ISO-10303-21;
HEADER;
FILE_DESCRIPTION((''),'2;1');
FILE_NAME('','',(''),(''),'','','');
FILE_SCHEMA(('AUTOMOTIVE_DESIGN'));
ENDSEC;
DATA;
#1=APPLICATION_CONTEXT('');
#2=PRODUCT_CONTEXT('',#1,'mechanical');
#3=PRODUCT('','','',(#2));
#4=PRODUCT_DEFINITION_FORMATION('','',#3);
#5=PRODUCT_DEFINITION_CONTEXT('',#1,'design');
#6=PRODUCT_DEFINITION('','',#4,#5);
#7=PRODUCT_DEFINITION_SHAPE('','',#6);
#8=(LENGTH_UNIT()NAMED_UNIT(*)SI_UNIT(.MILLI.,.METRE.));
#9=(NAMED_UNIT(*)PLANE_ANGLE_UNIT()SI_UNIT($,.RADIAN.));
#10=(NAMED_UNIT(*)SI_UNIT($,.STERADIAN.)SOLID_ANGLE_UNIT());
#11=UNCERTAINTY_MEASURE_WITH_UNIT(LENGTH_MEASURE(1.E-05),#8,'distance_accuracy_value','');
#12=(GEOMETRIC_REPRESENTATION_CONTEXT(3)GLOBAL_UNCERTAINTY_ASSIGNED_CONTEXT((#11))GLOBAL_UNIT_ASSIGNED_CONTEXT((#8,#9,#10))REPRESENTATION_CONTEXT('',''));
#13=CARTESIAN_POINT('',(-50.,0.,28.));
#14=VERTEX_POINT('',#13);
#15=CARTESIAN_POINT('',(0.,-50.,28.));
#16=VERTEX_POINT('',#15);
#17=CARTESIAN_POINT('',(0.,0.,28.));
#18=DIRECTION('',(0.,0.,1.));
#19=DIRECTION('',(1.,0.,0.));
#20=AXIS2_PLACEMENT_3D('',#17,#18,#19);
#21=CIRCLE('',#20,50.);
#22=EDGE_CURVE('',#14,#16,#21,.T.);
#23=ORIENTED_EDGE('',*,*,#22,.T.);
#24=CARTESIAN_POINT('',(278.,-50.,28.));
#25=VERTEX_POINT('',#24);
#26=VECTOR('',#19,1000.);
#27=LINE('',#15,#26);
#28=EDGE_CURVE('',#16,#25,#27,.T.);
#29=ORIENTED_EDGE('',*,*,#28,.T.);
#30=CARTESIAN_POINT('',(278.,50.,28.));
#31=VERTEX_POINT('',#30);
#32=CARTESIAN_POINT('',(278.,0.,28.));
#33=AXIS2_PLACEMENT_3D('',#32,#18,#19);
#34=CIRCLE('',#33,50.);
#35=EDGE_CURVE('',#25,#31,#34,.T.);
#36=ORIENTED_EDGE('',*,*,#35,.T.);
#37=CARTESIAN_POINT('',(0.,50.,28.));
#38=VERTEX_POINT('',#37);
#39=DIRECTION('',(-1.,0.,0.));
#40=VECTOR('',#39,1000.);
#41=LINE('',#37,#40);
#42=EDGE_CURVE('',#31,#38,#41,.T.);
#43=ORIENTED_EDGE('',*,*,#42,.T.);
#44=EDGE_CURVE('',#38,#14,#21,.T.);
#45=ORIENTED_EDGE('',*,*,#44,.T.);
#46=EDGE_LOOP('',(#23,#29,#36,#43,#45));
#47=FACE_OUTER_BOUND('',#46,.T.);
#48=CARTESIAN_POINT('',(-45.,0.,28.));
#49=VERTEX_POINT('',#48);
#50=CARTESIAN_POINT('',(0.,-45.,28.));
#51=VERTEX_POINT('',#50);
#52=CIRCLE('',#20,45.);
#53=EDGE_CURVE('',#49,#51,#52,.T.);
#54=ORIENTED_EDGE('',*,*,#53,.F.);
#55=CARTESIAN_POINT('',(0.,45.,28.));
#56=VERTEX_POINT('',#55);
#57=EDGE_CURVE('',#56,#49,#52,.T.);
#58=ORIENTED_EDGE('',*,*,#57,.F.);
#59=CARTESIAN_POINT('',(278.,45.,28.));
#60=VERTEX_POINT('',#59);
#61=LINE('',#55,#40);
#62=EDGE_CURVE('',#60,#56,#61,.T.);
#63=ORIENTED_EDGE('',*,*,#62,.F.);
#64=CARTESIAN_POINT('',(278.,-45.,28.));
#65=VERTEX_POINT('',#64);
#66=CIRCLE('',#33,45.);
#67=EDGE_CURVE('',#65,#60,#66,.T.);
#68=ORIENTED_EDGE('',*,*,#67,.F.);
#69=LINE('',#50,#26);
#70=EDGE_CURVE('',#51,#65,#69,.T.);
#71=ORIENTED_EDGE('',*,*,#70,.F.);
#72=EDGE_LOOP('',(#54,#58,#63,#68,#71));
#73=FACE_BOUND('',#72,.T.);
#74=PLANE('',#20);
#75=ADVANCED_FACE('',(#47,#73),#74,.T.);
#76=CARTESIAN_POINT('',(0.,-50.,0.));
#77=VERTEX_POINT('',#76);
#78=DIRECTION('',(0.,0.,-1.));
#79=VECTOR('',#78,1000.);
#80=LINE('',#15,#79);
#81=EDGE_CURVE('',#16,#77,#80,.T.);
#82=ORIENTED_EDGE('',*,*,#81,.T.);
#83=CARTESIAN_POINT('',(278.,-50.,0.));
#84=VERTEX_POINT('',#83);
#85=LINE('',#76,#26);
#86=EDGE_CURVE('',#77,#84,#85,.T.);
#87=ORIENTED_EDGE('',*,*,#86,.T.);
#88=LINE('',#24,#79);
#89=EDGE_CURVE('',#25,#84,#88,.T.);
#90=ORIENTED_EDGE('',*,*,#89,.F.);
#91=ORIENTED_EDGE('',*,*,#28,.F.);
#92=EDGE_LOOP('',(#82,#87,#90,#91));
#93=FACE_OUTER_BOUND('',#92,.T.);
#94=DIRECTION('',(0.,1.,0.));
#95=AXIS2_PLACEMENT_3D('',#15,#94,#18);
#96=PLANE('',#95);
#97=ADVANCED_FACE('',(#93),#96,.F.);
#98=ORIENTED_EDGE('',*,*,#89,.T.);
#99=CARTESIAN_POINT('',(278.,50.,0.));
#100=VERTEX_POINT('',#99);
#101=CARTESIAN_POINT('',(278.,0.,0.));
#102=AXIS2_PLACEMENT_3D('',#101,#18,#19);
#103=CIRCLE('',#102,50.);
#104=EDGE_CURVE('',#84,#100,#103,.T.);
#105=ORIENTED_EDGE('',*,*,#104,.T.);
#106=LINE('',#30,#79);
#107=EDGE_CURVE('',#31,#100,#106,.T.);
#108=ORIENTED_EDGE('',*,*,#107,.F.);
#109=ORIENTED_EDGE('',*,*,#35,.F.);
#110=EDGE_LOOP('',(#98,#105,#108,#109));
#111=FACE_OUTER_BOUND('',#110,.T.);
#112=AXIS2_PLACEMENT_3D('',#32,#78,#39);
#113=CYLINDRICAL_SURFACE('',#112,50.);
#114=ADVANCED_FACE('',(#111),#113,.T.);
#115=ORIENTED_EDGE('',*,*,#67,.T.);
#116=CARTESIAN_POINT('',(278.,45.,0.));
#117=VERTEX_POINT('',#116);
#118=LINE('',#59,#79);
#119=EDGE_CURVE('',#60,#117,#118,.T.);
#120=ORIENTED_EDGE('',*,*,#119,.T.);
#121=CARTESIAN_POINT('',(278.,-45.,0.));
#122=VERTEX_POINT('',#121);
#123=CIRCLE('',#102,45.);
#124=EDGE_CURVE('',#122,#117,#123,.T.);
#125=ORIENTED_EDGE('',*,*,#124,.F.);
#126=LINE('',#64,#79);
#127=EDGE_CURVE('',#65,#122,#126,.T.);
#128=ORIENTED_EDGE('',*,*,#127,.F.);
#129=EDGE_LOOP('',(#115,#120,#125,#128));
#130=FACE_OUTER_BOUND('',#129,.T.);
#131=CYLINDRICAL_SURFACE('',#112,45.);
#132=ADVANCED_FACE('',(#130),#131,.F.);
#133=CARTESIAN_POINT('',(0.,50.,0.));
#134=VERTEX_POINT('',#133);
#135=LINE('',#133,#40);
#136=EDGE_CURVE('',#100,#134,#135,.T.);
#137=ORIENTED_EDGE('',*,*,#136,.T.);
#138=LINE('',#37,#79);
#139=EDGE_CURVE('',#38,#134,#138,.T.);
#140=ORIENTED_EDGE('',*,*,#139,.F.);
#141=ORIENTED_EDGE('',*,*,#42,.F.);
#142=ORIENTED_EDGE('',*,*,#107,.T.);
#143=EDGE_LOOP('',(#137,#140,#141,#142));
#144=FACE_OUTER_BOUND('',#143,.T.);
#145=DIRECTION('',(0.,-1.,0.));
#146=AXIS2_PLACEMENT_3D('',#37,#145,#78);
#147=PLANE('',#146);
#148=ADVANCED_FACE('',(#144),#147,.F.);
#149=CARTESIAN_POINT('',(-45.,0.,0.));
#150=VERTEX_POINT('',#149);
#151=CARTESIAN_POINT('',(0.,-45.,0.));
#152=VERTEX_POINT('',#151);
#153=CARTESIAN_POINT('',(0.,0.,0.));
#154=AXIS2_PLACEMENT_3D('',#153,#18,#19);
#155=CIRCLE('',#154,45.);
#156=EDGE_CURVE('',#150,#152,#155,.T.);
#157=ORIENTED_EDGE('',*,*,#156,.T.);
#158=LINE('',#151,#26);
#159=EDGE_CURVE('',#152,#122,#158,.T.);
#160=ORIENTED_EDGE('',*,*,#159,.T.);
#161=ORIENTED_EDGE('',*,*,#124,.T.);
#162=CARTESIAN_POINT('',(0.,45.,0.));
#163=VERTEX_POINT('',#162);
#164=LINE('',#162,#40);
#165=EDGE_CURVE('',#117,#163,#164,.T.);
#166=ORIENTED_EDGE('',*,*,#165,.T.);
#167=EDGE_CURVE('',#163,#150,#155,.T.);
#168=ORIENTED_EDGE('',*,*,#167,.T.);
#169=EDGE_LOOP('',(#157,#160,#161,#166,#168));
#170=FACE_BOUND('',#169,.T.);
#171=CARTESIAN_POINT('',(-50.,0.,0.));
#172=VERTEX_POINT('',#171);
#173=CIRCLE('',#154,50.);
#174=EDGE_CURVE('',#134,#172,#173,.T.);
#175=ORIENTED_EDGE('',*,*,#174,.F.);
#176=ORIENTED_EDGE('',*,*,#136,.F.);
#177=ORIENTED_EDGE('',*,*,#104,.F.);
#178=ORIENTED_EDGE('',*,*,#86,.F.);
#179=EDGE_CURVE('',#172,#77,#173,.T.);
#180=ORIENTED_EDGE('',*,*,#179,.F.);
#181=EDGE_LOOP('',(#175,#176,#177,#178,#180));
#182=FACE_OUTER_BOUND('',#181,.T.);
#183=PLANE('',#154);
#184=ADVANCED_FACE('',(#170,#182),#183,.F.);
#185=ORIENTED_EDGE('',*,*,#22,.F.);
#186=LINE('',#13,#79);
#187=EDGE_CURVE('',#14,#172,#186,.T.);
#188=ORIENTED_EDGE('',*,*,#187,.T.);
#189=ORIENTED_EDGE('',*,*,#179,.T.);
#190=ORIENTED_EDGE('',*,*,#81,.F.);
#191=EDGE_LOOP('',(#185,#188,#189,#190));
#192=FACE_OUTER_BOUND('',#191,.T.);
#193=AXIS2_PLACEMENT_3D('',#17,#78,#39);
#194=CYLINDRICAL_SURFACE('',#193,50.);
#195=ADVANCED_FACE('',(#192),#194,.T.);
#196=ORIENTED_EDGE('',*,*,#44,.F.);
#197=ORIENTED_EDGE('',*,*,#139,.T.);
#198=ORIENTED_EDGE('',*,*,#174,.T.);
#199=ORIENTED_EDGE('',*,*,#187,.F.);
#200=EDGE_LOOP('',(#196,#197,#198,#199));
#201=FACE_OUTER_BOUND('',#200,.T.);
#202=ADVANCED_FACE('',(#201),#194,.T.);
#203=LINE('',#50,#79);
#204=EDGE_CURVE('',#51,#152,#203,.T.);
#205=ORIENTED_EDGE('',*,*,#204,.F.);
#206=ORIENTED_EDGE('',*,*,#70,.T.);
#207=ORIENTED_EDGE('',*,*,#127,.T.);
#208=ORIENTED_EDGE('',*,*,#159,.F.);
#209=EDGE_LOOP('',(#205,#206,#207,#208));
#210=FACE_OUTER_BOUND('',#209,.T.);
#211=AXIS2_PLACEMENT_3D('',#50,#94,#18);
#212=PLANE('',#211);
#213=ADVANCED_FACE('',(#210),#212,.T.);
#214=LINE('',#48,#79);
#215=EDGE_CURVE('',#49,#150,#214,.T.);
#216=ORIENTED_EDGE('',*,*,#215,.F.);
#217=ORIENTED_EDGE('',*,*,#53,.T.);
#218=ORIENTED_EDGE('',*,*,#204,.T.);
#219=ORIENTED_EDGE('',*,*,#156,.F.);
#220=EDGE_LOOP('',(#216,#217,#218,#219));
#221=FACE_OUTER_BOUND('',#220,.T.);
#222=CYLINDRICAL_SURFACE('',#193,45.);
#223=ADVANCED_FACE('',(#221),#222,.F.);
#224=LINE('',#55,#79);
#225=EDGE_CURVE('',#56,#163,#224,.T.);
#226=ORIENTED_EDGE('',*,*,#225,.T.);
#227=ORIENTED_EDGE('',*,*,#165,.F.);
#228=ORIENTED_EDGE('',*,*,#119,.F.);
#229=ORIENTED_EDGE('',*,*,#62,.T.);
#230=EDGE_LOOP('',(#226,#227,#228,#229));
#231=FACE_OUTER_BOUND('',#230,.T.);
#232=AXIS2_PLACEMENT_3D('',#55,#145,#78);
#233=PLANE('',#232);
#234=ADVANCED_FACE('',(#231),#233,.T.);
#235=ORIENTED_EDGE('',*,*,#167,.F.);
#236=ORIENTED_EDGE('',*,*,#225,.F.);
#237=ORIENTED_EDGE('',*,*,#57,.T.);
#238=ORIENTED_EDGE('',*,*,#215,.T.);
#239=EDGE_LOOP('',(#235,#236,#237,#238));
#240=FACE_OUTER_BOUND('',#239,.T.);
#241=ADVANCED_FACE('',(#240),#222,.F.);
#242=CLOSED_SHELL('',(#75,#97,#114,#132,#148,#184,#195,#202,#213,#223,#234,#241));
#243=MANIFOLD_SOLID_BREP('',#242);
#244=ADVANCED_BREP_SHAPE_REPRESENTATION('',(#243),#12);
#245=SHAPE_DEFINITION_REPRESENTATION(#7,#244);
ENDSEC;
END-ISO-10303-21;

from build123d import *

# Parameters (mm, degrees)
EXTRUDE_1_DEPTH = 28


with BuildPart() as part:
    # 草图1 → 凸台-拉伸1 (new body)
    with BuildSketch(Plane.XY):
        with BuildLine():
            Line((0, 50), (278, 50))
            ThreePointArc((278, 50), (328, 0), (278, -50))
            Line((278, -50), (0, -50))
            ThreePointArc((0, -50), (-50, 0), (0, 50))
        make_face()
        with BuildLine():
            Line((0, 45), (278, 45))
            ThreePointArc((278, 45), (323, 0), (278, -45))
            Line((278, -45), (0, -45))
            ThreePointArc((0, -45), (-45, 0), (0, 45))
        make_face(mode=Mode.SUBTRACT)
    extrude(amount=EXTRUDE_1_DEPTH)


solid = part.part
